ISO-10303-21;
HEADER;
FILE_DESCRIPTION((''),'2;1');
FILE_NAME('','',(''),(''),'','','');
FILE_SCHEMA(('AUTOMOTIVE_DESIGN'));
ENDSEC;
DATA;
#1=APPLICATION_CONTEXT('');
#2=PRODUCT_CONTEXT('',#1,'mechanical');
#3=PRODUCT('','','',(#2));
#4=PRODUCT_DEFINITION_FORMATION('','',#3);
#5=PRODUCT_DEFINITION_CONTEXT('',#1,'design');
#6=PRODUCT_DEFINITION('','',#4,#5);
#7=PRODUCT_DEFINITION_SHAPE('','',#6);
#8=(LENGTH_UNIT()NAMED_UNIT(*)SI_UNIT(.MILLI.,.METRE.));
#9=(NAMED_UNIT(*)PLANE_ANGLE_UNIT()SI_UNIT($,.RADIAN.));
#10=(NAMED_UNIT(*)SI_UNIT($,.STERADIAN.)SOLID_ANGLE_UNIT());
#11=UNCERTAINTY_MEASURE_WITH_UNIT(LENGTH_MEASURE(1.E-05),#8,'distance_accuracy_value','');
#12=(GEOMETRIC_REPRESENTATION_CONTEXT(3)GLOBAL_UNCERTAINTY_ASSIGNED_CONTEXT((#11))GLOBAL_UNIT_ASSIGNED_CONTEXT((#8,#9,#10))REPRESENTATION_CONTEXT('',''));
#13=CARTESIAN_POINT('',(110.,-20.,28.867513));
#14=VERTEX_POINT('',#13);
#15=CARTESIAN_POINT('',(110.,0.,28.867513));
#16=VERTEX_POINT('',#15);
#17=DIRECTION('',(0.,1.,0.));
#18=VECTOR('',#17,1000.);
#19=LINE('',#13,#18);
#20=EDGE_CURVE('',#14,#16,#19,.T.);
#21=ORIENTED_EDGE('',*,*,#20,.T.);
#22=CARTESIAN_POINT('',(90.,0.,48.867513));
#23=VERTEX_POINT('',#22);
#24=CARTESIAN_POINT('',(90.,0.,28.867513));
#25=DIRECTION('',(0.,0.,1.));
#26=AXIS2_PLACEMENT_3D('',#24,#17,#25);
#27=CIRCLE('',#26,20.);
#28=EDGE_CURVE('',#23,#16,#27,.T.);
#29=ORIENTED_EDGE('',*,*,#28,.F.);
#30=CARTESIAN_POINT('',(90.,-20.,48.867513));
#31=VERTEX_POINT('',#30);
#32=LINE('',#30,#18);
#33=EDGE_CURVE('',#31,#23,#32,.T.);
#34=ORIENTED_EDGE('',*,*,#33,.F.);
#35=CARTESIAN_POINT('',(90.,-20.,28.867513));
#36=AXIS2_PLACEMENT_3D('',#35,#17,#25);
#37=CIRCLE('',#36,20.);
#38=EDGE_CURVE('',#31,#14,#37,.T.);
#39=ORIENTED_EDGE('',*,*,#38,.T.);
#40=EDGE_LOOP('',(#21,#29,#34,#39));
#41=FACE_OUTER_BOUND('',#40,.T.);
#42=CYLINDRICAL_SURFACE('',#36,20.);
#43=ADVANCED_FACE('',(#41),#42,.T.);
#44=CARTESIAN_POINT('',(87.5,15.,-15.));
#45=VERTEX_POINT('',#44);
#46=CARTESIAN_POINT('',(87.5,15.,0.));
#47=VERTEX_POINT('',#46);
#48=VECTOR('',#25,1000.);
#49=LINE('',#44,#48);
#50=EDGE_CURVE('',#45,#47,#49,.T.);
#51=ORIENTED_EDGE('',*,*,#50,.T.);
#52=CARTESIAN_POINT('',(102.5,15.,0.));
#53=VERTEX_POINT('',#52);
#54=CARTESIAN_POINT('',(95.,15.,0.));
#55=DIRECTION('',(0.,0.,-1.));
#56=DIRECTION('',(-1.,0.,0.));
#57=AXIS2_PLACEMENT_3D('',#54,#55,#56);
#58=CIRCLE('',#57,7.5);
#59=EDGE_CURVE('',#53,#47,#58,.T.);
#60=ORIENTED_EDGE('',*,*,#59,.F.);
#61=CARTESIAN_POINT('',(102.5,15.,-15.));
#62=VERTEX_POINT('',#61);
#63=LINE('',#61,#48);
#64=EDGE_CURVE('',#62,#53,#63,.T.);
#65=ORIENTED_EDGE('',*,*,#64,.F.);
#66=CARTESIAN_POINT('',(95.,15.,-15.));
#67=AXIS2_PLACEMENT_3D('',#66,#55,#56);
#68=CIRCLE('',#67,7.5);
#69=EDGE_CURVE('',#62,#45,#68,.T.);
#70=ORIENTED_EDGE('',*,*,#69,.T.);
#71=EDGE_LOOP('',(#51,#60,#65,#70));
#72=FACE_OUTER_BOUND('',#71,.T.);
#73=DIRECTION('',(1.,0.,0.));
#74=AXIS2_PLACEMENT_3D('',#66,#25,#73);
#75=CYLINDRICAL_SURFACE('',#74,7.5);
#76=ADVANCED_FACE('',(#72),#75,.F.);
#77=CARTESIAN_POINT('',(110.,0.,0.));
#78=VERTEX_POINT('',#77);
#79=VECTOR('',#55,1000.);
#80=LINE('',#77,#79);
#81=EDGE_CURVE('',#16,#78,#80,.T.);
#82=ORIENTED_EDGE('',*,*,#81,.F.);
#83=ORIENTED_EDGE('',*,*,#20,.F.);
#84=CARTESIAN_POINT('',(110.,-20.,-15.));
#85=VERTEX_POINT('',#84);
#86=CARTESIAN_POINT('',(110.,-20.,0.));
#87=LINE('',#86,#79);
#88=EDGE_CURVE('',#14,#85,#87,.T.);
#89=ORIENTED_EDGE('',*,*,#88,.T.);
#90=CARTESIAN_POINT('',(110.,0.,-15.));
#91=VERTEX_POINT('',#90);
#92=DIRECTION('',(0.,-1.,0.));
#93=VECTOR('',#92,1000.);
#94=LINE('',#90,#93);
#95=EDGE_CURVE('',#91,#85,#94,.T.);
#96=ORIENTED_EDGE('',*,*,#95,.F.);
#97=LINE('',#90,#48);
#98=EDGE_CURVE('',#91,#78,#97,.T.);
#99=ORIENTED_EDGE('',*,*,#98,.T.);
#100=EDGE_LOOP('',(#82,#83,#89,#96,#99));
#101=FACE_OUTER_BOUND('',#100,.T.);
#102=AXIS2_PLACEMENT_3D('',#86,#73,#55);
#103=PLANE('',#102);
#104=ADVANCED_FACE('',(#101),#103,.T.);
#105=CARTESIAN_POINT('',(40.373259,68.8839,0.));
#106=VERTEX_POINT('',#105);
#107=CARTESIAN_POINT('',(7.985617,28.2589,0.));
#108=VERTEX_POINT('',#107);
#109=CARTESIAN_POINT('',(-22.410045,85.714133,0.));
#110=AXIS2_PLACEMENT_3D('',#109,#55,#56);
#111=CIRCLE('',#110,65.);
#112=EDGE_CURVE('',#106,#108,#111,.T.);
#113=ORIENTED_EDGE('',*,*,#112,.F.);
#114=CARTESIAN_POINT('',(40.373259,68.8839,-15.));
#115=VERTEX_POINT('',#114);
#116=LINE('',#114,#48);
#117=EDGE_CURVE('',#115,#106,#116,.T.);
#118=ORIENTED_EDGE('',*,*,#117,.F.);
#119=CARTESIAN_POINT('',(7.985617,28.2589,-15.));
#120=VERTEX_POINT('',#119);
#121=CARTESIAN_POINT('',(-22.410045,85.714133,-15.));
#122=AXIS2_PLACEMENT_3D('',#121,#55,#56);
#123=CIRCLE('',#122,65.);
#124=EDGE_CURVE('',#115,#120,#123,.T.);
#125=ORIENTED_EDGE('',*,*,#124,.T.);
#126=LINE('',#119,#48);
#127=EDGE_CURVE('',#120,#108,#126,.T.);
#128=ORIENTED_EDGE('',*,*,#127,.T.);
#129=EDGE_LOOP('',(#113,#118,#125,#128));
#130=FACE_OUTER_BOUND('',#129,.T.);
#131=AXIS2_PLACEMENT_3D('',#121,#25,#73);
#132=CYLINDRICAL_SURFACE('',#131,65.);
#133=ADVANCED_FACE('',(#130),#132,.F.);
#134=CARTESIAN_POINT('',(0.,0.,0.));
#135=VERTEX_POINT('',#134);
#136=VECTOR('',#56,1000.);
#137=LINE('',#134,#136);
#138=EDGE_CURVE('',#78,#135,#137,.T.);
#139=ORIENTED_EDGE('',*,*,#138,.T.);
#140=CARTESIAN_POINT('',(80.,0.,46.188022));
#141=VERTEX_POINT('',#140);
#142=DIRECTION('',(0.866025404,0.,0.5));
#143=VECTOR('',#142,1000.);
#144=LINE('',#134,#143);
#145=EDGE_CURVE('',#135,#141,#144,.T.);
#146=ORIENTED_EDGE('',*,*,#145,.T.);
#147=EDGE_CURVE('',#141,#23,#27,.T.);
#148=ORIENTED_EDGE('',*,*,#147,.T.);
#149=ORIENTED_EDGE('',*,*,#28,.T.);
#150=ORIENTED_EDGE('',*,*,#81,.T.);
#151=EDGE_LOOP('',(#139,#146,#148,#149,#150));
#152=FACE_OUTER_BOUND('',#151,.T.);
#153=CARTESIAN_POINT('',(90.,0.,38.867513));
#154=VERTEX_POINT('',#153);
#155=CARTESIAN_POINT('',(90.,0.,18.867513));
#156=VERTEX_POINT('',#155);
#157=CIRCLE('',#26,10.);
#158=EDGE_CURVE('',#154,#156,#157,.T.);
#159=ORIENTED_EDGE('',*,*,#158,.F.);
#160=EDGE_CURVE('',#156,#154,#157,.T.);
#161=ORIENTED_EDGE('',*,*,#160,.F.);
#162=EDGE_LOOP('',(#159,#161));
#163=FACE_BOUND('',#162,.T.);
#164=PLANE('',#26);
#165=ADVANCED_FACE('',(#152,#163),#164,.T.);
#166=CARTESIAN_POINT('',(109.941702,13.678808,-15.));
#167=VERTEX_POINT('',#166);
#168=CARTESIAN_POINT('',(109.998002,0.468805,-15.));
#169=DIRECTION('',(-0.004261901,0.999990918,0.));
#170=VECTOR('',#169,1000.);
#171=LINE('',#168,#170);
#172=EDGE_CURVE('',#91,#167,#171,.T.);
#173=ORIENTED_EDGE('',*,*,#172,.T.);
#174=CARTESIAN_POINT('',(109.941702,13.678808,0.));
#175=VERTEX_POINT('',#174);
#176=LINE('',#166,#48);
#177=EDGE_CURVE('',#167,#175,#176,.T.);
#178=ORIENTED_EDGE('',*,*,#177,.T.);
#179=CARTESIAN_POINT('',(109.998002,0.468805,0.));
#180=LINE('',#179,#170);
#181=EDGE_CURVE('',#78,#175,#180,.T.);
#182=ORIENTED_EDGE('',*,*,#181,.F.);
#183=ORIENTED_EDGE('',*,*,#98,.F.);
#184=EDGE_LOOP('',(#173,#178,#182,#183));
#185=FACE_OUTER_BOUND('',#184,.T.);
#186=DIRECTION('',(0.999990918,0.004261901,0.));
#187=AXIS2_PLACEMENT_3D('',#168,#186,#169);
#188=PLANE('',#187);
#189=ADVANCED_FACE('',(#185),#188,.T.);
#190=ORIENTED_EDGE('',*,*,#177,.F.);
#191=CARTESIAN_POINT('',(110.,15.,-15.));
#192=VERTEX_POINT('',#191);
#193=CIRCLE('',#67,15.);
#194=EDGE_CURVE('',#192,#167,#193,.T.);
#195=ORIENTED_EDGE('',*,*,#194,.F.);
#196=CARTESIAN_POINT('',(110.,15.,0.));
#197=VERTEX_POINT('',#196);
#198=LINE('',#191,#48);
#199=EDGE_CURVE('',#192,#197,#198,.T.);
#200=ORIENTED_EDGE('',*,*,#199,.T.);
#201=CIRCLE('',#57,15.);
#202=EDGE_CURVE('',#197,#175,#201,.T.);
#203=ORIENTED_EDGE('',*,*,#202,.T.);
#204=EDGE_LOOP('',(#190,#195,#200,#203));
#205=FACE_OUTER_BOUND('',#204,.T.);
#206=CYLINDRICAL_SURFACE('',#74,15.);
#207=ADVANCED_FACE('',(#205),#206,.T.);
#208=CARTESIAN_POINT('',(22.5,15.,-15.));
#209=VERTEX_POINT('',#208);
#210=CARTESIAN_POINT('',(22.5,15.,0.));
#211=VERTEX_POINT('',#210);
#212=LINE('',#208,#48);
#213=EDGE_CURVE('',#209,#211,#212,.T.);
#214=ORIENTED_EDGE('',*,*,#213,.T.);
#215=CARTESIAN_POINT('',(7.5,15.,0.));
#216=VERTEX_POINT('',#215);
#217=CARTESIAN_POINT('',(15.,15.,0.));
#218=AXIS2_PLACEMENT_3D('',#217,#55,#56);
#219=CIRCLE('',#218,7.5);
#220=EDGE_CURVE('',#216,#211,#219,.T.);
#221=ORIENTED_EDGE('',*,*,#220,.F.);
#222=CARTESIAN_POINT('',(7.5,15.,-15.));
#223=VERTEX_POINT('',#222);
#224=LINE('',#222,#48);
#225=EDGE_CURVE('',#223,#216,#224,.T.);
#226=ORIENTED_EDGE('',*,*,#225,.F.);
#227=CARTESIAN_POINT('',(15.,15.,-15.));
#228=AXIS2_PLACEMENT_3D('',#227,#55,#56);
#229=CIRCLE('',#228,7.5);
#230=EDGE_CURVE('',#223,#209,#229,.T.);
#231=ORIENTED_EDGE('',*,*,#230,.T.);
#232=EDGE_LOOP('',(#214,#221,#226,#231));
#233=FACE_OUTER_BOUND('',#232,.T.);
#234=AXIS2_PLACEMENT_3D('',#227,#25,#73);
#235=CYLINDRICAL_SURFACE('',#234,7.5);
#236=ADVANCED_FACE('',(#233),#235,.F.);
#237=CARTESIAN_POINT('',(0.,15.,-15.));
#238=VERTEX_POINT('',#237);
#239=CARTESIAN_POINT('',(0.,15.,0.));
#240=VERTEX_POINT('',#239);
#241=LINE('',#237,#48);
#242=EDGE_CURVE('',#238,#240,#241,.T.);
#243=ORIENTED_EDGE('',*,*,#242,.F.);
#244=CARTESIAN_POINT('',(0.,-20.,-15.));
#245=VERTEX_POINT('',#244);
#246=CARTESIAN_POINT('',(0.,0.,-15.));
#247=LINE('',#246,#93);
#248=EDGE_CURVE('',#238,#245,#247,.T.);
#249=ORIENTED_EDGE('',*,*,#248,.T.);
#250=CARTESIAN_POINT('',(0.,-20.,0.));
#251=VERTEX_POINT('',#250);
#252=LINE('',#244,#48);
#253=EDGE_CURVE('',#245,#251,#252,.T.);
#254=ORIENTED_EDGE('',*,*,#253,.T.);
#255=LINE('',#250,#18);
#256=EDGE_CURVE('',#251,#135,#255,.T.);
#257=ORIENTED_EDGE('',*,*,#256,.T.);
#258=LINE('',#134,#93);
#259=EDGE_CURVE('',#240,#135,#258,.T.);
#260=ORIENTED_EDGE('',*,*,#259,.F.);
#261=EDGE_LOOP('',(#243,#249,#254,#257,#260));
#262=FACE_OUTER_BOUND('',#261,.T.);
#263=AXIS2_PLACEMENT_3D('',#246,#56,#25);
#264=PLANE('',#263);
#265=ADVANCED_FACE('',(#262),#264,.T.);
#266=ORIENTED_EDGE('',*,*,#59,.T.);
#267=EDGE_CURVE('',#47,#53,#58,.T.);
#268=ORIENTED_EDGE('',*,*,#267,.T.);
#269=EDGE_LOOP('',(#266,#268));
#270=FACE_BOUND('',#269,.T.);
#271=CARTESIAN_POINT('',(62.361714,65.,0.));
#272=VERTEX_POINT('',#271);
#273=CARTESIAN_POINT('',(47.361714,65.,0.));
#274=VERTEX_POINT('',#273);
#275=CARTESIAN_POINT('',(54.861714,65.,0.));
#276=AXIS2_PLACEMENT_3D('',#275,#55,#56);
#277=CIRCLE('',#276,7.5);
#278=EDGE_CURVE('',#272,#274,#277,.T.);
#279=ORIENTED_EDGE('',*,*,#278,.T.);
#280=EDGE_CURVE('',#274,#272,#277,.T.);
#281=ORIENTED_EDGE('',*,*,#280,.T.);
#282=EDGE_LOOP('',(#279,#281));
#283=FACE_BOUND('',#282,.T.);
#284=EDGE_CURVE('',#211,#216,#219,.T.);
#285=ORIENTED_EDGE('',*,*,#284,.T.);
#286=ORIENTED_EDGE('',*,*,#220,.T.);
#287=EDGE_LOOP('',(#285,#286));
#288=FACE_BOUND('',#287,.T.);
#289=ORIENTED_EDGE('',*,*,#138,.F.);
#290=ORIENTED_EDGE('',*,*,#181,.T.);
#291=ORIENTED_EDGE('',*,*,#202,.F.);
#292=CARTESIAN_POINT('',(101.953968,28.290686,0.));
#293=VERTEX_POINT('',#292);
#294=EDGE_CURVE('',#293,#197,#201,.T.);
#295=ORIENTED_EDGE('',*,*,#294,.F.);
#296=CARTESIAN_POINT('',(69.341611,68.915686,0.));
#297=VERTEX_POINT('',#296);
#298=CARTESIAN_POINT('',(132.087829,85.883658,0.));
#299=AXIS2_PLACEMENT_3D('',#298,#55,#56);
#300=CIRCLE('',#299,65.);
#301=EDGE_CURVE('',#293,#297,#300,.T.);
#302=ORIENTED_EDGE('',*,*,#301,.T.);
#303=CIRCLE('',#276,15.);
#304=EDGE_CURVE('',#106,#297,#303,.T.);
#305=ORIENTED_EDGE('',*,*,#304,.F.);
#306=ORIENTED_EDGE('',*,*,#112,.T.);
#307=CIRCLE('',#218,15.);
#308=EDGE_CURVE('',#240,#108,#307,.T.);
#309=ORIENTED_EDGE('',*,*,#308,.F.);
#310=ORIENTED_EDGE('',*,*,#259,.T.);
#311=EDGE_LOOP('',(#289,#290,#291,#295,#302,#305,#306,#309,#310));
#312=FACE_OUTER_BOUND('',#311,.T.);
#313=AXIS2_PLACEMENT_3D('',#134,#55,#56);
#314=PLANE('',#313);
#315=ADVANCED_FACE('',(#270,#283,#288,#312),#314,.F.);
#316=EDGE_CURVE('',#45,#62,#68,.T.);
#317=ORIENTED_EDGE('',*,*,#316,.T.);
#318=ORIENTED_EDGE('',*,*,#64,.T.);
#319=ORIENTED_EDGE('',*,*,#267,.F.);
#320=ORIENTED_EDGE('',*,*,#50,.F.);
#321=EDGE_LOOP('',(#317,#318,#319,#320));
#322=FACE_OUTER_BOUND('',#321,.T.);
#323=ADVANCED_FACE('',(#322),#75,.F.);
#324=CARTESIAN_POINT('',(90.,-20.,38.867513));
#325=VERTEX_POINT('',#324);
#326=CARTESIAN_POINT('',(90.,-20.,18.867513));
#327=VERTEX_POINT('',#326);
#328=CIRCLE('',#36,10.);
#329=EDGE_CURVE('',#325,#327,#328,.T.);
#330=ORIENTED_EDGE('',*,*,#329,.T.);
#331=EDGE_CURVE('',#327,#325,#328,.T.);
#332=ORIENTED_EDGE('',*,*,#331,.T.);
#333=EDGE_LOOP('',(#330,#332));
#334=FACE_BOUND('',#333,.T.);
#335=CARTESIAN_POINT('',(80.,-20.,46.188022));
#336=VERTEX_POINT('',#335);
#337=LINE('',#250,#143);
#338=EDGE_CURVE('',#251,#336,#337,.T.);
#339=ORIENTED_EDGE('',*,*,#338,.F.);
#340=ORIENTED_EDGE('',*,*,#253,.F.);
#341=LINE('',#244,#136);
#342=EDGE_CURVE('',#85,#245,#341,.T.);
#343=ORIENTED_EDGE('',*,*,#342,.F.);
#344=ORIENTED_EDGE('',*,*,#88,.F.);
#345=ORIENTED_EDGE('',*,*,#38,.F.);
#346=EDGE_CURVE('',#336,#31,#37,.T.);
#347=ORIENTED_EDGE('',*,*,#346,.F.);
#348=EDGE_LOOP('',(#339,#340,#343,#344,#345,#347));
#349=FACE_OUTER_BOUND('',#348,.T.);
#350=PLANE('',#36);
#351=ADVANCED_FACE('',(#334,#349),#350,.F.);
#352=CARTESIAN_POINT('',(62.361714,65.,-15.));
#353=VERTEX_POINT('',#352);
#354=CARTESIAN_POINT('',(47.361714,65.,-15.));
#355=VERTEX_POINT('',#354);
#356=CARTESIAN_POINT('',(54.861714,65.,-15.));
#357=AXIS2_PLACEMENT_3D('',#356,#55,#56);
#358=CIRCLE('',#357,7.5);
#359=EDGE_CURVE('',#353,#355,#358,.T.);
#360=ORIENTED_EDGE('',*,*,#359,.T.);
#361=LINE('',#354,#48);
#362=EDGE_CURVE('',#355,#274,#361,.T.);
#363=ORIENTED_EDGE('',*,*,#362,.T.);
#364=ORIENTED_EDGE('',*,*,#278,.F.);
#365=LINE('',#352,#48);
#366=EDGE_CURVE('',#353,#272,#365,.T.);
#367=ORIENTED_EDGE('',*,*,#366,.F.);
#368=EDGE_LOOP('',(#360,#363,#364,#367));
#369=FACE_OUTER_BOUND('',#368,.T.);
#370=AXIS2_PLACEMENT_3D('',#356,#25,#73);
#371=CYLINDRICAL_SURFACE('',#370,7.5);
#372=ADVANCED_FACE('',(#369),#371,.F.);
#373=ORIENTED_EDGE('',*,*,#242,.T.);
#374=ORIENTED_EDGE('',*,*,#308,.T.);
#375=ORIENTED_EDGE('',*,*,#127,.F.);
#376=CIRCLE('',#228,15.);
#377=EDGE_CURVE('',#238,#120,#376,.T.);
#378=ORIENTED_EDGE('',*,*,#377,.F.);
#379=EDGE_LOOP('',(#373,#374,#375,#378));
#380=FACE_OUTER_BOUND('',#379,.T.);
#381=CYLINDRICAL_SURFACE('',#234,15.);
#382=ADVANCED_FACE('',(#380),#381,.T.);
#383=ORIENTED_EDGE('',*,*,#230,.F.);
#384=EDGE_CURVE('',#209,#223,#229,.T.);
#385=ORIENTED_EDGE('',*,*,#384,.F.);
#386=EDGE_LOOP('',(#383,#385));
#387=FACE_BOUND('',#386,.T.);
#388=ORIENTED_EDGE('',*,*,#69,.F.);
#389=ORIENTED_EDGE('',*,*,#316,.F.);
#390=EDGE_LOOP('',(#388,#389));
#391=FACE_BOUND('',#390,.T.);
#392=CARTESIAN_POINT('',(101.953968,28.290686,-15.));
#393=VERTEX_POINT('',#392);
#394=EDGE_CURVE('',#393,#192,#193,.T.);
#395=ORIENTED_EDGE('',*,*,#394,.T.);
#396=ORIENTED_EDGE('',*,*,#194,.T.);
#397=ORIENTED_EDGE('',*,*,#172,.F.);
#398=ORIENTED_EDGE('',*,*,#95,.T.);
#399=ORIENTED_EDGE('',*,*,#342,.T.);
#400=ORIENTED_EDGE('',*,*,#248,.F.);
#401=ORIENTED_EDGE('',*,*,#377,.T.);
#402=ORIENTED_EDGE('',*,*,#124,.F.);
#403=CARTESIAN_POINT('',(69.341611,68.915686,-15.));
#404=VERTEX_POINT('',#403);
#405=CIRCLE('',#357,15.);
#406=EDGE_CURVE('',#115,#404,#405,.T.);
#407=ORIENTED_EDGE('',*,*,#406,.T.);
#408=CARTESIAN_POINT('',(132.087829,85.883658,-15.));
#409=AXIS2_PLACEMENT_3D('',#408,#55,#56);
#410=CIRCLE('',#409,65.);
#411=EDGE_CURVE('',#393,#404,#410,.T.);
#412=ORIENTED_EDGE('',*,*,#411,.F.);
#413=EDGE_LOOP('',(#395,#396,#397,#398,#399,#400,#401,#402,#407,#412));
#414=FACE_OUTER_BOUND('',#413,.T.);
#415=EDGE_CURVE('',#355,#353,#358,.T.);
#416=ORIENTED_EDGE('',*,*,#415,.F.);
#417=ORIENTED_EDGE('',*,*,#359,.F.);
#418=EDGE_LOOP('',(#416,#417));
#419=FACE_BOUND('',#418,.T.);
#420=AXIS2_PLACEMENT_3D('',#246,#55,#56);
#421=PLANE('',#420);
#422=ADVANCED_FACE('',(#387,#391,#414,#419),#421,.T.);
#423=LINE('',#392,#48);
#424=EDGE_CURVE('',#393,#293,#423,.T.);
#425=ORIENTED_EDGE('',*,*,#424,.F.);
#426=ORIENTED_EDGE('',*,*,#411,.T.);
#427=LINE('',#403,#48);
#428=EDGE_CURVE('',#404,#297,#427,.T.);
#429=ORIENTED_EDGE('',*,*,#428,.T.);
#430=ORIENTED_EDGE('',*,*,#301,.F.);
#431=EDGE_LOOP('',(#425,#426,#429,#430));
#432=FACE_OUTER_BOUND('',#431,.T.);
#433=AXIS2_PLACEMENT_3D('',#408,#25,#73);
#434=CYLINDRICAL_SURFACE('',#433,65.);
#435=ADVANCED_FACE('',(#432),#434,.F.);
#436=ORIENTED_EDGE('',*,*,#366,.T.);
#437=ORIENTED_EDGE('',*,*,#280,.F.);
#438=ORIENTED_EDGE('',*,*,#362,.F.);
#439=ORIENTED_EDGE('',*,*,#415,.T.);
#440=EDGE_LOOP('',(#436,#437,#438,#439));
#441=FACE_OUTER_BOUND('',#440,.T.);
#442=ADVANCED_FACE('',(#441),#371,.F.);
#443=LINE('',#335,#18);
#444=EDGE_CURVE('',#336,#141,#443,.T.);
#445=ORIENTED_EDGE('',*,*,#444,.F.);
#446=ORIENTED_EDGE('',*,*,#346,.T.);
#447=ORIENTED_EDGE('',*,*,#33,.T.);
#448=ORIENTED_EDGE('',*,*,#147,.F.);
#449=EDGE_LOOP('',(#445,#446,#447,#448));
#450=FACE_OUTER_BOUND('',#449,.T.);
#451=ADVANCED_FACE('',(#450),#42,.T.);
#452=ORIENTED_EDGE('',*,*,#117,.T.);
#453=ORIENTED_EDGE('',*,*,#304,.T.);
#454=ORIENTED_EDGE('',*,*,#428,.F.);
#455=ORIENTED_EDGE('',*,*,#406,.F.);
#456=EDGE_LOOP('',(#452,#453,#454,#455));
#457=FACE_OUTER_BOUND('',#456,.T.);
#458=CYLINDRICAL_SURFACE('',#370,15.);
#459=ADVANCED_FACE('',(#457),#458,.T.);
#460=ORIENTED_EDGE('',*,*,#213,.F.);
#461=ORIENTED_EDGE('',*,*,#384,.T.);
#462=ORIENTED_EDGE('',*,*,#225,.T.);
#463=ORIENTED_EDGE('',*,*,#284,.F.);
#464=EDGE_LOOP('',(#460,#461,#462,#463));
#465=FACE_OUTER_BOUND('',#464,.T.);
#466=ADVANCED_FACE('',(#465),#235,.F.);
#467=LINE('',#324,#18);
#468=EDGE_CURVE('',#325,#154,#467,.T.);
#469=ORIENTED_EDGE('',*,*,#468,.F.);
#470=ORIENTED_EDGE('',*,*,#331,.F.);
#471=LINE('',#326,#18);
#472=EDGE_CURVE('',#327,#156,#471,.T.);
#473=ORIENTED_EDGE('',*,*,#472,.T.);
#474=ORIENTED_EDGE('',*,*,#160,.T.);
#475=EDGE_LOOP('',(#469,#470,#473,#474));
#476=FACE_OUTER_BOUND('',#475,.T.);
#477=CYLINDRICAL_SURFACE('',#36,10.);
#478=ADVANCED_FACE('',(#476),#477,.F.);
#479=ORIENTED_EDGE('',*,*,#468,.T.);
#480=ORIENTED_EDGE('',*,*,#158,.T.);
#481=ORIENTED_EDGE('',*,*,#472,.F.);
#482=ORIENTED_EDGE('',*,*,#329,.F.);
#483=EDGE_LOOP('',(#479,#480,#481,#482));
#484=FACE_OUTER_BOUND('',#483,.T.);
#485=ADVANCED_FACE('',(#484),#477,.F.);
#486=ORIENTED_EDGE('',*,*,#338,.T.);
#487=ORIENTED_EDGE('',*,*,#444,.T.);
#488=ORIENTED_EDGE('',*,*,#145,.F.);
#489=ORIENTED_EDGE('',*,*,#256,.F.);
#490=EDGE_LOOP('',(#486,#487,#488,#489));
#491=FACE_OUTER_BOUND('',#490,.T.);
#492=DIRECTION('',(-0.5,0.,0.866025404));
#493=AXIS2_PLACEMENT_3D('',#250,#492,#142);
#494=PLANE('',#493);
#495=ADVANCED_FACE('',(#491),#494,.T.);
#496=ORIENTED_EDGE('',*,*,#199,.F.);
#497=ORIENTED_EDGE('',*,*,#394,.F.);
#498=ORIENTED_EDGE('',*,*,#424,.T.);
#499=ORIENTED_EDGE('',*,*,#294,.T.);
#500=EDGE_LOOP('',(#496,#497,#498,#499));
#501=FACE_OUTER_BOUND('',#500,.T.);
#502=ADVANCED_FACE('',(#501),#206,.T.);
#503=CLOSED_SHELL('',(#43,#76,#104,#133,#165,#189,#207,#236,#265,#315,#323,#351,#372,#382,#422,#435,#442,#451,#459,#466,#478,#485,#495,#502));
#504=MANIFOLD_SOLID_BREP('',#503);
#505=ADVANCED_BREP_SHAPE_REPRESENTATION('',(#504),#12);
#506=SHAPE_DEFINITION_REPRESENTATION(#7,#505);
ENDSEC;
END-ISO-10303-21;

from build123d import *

# Parameters (mm, degrees)
BASE_WEDGE_PROFILE_SKETCH_R     = 10
BASE_WEDGE_BLOCK_DEPTH          = 20
UPRIGHT_FLANGE_PROFILE_SKETCH_R = 7.5
UPRIGHT_FLANGE_PROFILE_SKETCH_W = 110
UPRIGHT_FLANGE_PROFILE_SKETCH_H = 20
UPRIGHT_FLANGE_WITH_HOLES_DEPTH = 15


with BuildPart() as part:
    # Base Wedge Profile Sketch → Base Wedge Block (new body)
    with BuildSketch(Plane(origin=(0, 0, 0), x_dir=(1, 0, 0), z_dir=(0, 1, 0))):
        with BuildLine():
            Line((0, 0), (110, 0))
            Line((110, 0), (110, -28.867513459))
            ThreePointArc((110, -28.867513459), (100, -46.188021535), (80, -46.188021535))
            Line((80, -46.188021535), (0, 0))
        make_face()
        with Locations(Location((90, -28.867513459, 0), (0, 0, 270))):
            Circle(BASE_WEDGE_PROFILE_SKETCH_R, mode=Mode.SUBTRACT)
    extrude(amount=-BASE_WEDGE_BLOCK_DEPTH)

    # Upright Flange Profile Sketch → Upright Flange with Holes (add)
    # profile 1 of 2: a face of its own
    with BuildSketch(Plane(origin=(0, 0, 0), x_dir=(-1, 0, 0), z_dir=(0, 0, -1))):
        with BuildLine():
            ThreePointArc((-40.373259229, 68.883899859), (-28.414925005, 45.194724357), (-7.985616598, 28.258899859))
            ThreePointArc((-7.985616598, 28.258899859), (-2.150569059, 22.739000225), (0, 15))
            Line((0, 15), (0, 0))
            Line((0, 0), (-110, 0))
            Line((-110, 0), (-109.941701745, 13.678807753))
            ThreePointArc((-109.941701745, 13.678807753), (-108.161756455, 22.195009869), (-101.953967939, 28.290685833))
            ThreePointArc((-101.953967939, 28.290685833), (-81.399813181, 45.193056262), (-69.341610571, 68.915685833))
            ThreePointArc((-69.341610571, 68.915685833), (-54.845255035, 79.99999097), (-40.373259229, 68.883899859))
        make_face()
        with Locations((-54.861714008, 65)):
            Circle(UPRIGHT_FLANGE_PROFILE_SKETCH_R, mode=Mode.SUBTRACT)
        with Locations((-15, 15)):
            Circle(UPRIGHT_FLANGE_PROFILE_SKETCH_R, mode=Mode.SUBTRACT)
        with Locations((-95, 15)):
            Circle(UPRIGHT_FLANGE_PROFILE_SKETCH_R, mode=Mode.SUBTRACT)
    # profile 2 of 2: a face of its own
    with BuildSketch(Plane(origin=(0, 0, 0), x_dir=(-1, 0, 0), z_dir=(0, 0, -1))):
        with Locations((-55, -10)):
            Rectangle(UPRIGHT_FLANGE_PROFILE_SKETCH_W, UPRIGHT_FLANGE_PROFILE_SKETCH_H)
    extrude(amount=UPRIGHT_FLANGE_WITH_HOLES_DEPTH)


solid = part.part
